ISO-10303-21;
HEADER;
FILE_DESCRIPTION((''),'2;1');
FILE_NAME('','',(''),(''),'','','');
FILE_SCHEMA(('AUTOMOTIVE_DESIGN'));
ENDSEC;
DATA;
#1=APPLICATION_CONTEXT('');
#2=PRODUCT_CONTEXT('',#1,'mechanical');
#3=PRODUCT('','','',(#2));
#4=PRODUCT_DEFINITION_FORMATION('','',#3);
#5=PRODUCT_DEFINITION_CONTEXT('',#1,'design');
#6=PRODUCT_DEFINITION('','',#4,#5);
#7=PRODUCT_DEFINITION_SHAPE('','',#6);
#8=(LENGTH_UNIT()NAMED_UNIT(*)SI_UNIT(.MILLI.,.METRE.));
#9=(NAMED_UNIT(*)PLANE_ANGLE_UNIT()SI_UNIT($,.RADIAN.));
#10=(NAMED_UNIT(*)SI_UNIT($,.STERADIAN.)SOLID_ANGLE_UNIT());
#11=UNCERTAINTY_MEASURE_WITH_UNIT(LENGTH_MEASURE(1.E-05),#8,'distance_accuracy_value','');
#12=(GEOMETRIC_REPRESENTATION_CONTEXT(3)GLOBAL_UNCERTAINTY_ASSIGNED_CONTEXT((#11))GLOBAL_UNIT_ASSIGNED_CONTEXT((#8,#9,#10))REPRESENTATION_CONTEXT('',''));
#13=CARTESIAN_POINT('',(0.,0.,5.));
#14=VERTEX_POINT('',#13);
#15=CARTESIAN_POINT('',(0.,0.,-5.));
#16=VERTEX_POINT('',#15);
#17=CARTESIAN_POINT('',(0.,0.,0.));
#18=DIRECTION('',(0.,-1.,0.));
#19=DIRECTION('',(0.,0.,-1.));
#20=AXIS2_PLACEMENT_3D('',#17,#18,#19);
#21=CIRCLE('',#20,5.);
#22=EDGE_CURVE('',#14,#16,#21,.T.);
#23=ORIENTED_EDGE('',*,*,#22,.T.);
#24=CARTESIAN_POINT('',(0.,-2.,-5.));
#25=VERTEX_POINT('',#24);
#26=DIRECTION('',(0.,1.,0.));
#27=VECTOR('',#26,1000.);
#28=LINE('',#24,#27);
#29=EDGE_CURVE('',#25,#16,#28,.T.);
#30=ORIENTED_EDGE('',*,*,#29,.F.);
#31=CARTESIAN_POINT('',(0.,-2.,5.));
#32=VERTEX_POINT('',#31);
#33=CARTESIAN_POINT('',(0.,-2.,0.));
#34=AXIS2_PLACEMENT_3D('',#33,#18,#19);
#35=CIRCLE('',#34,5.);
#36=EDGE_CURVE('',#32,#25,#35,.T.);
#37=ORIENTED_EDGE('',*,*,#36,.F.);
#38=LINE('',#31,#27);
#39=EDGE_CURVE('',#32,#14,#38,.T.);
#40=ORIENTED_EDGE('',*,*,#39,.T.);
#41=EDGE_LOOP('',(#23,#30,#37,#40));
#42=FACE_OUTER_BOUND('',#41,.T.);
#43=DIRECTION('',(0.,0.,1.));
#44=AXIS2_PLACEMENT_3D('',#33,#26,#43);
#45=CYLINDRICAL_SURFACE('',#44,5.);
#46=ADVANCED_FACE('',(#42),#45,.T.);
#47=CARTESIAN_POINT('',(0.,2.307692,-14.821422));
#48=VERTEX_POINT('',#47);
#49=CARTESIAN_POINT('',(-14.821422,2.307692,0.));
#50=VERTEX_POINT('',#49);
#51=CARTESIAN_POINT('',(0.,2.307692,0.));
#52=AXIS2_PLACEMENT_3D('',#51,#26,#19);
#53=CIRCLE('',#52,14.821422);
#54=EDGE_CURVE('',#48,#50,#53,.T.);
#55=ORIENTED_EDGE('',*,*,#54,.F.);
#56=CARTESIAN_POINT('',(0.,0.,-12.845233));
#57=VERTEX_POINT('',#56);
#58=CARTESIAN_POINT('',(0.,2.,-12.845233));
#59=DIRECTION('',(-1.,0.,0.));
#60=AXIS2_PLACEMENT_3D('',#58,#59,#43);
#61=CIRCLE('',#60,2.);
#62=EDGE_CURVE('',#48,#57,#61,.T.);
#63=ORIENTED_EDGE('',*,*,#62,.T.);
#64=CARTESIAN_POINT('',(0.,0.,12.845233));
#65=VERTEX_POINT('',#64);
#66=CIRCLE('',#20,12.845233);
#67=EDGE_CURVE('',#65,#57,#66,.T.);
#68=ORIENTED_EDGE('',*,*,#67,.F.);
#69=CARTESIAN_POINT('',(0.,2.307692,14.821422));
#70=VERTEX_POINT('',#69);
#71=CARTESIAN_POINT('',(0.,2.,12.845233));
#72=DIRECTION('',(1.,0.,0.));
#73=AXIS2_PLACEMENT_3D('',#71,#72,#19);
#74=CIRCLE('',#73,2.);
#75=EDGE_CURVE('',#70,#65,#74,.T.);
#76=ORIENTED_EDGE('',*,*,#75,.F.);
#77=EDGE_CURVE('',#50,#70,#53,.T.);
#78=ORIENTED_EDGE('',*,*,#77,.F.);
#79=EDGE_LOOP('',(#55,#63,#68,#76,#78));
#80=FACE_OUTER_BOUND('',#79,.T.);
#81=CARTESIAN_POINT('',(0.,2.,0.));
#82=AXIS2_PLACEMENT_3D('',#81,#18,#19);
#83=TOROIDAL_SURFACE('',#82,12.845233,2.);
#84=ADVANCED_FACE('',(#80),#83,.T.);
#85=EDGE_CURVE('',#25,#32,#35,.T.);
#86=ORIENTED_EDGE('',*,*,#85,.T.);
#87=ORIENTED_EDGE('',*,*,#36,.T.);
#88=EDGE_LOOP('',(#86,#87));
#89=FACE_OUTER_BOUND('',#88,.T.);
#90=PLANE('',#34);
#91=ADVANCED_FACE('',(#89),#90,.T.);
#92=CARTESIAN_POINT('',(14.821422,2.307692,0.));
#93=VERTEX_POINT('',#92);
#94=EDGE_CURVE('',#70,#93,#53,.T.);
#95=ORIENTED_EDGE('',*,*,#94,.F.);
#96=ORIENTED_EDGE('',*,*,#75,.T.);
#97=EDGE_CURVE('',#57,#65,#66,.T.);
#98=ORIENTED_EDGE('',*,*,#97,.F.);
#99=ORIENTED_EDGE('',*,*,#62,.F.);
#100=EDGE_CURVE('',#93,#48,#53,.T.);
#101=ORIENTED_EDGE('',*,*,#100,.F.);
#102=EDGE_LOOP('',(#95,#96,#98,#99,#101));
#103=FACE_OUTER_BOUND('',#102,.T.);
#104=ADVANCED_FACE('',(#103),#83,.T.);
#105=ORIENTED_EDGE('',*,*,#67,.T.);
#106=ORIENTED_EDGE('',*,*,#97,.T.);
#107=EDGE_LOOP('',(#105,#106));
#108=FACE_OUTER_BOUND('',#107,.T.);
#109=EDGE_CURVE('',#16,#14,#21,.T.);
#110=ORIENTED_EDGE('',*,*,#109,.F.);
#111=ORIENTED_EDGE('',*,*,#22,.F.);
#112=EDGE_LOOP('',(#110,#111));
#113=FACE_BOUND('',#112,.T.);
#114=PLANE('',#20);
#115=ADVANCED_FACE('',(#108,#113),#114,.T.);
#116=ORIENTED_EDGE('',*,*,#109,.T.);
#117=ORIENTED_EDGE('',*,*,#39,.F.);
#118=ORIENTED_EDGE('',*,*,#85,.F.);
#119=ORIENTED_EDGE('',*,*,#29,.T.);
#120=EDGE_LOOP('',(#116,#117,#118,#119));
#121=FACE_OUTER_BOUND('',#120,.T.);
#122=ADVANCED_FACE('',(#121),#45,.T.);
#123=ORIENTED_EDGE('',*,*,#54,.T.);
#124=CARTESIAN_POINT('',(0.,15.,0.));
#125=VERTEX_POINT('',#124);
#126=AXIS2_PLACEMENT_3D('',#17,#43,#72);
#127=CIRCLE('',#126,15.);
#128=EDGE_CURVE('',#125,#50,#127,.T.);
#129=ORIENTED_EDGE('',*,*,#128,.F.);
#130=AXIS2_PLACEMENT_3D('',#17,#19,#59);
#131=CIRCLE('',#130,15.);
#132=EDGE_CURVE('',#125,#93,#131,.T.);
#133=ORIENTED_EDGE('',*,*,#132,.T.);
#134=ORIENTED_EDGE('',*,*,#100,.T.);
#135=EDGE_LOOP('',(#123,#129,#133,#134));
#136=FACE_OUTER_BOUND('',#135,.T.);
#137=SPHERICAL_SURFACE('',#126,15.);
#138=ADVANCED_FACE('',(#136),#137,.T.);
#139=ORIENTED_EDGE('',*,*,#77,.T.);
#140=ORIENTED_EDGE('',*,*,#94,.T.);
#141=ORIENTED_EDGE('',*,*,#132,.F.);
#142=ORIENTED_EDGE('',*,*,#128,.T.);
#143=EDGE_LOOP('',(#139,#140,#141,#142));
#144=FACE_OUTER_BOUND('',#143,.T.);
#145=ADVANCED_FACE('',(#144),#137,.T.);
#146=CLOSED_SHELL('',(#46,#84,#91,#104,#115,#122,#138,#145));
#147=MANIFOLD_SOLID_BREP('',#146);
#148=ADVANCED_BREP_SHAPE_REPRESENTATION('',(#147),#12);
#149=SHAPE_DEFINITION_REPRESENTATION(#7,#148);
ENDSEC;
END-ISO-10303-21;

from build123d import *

# Parameters (mm, degrees)
SKETCH_2_R      = 5
EXTRUDE_1_DEPTH = 2
FILLET_1_R      = 2


with BuildPart() as part:
    # 草图1 → 旋转1 (revolve)
    with BuildSketch(Plane.XY):
        with BuildLine():
            Line((0, 15), (0, 0))
            Line((0, 0), (15, 0))
            ThreePointArc((15, 0), (10.606601718, 10.606601718), (0, 15))
        make_face()
    revolve(axis=Axis((0, 0, 0), (0, 1, 0)))

    # 草图2 → 凸台-拉伸1 (add)
    with BuildSketch(Plane.XZ):
        with Locations(Location((0, 0, 0), (0, 0, 270))):
            Circle(SKETCH_2_R)
    extrude(amount=EXTRUDE_1_DEPTH)

    # 圆角1
    fillet_1_edges = [part.edges().sort_by_distance(p)[0] for p in [
        (-15, 0, 0),
    ]]
    fillet(fillet_1_edges, radius=FILLET_1_R)


solid = part.part
